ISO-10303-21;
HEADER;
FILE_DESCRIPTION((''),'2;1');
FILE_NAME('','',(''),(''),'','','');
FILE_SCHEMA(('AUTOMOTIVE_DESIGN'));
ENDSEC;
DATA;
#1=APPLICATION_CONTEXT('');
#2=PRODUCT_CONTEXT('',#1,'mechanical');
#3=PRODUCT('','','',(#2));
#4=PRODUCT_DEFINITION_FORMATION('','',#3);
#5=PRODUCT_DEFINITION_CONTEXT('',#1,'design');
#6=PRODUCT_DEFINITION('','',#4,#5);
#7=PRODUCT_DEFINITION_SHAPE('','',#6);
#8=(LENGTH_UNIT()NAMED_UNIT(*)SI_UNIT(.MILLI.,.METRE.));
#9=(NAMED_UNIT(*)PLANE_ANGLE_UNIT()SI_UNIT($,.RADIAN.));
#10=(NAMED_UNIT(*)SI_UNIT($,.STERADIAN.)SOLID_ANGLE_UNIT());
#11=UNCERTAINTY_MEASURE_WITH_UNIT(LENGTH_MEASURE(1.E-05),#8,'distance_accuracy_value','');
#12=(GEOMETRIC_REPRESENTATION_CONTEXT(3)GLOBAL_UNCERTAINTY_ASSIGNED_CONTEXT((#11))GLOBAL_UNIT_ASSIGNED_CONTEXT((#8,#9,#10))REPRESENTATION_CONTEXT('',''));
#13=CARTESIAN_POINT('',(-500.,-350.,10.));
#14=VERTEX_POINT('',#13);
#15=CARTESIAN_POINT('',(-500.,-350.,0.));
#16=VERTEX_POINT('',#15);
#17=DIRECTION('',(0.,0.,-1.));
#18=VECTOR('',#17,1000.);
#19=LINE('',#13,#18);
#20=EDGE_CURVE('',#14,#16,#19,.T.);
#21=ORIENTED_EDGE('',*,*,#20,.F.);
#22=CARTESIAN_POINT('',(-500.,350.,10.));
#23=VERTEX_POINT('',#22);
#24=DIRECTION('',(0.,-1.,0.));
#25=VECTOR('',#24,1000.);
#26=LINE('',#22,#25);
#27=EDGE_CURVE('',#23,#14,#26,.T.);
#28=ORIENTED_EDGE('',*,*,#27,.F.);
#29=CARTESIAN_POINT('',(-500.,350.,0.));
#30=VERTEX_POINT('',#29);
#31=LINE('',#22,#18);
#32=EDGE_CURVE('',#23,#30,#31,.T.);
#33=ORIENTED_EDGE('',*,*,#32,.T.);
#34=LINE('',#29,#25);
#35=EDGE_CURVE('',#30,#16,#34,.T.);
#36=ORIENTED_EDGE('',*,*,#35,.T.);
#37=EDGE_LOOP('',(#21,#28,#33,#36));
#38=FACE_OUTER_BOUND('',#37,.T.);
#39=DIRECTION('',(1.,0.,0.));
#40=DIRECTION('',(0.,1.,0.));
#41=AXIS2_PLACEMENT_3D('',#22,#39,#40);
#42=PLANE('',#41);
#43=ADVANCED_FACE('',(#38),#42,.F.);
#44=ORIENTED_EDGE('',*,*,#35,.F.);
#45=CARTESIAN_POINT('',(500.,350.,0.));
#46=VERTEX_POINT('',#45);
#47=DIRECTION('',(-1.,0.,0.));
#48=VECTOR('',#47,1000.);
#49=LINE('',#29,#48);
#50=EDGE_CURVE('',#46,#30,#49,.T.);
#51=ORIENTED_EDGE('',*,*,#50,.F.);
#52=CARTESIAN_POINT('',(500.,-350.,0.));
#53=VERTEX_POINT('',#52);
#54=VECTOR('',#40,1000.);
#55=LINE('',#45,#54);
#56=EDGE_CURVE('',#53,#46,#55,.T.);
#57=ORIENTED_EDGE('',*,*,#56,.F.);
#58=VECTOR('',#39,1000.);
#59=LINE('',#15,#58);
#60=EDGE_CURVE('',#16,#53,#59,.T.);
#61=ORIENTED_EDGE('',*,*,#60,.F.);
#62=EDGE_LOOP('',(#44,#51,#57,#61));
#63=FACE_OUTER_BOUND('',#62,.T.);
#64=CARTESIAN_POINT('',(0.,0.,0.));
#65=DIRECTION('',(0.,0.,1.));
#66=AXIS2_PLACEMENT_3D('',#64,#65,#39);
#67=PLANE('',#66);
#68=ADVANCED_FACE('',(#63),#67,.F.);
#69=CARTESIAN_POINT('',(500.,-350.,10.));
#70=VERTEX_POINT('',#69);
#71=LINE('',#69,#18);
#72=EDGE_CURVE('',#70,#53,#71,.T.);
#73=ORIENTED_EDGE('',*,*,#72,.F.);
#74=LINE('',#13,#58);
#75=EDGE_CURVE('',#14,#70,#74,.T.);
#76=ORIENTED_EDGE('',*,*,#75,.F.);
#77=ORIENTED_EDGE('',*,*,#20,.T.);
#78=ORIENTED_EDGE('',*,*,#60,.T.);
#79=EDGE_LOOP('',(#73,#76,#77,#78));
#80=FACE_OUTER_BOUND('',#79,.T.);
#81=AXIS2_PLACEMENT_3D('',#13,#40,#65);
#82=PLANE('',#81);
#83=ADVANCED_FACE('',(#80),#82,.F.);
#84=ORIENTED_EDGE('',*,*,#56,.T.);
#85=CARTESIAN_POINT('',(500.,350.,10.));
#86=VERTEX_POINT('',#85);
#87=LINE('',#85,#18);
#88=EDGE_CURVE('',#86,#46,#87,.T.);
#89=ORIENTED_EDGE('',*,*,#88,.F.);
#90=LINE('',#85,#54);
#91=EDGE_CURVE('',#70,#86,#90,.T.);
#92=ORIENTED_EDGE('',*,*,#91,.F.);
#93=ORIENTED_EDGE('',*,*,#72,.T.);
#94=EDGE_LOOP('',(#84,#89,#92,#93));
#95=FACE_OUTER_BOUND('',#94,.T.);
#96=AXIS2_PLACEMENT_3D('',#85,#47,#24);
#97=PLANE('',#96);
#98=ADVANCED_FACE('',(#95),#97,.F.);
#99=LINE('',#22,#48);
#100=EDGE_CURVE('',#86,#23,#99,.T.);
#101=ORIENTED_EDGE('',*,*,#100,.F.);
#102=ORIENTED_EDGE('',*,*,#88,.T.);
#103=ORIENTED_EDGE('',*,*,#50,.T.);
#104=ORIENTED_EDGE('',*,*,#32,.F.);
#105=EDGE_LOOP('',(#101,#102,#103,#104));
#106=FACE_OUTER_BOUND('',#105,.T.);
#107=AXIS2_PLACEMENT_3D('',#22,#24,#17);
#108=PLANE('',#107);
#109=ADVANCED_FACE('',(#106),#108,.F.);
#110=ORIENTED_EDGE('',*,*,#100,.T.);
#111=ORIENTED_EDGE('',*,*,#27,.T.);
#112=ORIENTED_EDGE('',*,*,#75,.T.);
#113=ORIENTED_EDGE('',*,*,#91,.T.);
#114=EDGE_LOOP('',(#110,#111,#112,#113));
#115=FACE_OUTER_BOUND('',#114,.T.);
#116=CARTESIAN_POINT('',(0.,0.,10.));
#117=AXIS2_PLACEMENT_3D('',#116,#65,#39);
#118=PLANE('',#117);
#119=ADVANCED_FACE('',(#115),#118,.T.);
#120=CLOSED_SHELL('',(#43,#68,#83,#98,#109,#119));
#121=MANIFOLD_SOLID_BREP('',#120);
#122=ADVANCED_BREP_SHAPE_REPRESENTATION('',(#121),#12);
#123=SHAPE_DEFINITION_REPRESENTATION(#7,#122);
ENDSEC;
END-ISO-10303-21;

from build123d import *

# Parameters (mm, degrees)
SKETCH1_W           = 1000
SKETCH1_H           = 700
BOSS_EXTRUDE1_DEPTH = 10


with BuildPart() as part:
    # Sketch1 → Boss-Extrude1 (new body)
    with BuildSketch(Plane.XY):
        Rectangle(SKETCH1_W, SKETCH1_H)
    extrude(amount=BOSS_EXTRUDE1_DEPTH)


solid = part.part
